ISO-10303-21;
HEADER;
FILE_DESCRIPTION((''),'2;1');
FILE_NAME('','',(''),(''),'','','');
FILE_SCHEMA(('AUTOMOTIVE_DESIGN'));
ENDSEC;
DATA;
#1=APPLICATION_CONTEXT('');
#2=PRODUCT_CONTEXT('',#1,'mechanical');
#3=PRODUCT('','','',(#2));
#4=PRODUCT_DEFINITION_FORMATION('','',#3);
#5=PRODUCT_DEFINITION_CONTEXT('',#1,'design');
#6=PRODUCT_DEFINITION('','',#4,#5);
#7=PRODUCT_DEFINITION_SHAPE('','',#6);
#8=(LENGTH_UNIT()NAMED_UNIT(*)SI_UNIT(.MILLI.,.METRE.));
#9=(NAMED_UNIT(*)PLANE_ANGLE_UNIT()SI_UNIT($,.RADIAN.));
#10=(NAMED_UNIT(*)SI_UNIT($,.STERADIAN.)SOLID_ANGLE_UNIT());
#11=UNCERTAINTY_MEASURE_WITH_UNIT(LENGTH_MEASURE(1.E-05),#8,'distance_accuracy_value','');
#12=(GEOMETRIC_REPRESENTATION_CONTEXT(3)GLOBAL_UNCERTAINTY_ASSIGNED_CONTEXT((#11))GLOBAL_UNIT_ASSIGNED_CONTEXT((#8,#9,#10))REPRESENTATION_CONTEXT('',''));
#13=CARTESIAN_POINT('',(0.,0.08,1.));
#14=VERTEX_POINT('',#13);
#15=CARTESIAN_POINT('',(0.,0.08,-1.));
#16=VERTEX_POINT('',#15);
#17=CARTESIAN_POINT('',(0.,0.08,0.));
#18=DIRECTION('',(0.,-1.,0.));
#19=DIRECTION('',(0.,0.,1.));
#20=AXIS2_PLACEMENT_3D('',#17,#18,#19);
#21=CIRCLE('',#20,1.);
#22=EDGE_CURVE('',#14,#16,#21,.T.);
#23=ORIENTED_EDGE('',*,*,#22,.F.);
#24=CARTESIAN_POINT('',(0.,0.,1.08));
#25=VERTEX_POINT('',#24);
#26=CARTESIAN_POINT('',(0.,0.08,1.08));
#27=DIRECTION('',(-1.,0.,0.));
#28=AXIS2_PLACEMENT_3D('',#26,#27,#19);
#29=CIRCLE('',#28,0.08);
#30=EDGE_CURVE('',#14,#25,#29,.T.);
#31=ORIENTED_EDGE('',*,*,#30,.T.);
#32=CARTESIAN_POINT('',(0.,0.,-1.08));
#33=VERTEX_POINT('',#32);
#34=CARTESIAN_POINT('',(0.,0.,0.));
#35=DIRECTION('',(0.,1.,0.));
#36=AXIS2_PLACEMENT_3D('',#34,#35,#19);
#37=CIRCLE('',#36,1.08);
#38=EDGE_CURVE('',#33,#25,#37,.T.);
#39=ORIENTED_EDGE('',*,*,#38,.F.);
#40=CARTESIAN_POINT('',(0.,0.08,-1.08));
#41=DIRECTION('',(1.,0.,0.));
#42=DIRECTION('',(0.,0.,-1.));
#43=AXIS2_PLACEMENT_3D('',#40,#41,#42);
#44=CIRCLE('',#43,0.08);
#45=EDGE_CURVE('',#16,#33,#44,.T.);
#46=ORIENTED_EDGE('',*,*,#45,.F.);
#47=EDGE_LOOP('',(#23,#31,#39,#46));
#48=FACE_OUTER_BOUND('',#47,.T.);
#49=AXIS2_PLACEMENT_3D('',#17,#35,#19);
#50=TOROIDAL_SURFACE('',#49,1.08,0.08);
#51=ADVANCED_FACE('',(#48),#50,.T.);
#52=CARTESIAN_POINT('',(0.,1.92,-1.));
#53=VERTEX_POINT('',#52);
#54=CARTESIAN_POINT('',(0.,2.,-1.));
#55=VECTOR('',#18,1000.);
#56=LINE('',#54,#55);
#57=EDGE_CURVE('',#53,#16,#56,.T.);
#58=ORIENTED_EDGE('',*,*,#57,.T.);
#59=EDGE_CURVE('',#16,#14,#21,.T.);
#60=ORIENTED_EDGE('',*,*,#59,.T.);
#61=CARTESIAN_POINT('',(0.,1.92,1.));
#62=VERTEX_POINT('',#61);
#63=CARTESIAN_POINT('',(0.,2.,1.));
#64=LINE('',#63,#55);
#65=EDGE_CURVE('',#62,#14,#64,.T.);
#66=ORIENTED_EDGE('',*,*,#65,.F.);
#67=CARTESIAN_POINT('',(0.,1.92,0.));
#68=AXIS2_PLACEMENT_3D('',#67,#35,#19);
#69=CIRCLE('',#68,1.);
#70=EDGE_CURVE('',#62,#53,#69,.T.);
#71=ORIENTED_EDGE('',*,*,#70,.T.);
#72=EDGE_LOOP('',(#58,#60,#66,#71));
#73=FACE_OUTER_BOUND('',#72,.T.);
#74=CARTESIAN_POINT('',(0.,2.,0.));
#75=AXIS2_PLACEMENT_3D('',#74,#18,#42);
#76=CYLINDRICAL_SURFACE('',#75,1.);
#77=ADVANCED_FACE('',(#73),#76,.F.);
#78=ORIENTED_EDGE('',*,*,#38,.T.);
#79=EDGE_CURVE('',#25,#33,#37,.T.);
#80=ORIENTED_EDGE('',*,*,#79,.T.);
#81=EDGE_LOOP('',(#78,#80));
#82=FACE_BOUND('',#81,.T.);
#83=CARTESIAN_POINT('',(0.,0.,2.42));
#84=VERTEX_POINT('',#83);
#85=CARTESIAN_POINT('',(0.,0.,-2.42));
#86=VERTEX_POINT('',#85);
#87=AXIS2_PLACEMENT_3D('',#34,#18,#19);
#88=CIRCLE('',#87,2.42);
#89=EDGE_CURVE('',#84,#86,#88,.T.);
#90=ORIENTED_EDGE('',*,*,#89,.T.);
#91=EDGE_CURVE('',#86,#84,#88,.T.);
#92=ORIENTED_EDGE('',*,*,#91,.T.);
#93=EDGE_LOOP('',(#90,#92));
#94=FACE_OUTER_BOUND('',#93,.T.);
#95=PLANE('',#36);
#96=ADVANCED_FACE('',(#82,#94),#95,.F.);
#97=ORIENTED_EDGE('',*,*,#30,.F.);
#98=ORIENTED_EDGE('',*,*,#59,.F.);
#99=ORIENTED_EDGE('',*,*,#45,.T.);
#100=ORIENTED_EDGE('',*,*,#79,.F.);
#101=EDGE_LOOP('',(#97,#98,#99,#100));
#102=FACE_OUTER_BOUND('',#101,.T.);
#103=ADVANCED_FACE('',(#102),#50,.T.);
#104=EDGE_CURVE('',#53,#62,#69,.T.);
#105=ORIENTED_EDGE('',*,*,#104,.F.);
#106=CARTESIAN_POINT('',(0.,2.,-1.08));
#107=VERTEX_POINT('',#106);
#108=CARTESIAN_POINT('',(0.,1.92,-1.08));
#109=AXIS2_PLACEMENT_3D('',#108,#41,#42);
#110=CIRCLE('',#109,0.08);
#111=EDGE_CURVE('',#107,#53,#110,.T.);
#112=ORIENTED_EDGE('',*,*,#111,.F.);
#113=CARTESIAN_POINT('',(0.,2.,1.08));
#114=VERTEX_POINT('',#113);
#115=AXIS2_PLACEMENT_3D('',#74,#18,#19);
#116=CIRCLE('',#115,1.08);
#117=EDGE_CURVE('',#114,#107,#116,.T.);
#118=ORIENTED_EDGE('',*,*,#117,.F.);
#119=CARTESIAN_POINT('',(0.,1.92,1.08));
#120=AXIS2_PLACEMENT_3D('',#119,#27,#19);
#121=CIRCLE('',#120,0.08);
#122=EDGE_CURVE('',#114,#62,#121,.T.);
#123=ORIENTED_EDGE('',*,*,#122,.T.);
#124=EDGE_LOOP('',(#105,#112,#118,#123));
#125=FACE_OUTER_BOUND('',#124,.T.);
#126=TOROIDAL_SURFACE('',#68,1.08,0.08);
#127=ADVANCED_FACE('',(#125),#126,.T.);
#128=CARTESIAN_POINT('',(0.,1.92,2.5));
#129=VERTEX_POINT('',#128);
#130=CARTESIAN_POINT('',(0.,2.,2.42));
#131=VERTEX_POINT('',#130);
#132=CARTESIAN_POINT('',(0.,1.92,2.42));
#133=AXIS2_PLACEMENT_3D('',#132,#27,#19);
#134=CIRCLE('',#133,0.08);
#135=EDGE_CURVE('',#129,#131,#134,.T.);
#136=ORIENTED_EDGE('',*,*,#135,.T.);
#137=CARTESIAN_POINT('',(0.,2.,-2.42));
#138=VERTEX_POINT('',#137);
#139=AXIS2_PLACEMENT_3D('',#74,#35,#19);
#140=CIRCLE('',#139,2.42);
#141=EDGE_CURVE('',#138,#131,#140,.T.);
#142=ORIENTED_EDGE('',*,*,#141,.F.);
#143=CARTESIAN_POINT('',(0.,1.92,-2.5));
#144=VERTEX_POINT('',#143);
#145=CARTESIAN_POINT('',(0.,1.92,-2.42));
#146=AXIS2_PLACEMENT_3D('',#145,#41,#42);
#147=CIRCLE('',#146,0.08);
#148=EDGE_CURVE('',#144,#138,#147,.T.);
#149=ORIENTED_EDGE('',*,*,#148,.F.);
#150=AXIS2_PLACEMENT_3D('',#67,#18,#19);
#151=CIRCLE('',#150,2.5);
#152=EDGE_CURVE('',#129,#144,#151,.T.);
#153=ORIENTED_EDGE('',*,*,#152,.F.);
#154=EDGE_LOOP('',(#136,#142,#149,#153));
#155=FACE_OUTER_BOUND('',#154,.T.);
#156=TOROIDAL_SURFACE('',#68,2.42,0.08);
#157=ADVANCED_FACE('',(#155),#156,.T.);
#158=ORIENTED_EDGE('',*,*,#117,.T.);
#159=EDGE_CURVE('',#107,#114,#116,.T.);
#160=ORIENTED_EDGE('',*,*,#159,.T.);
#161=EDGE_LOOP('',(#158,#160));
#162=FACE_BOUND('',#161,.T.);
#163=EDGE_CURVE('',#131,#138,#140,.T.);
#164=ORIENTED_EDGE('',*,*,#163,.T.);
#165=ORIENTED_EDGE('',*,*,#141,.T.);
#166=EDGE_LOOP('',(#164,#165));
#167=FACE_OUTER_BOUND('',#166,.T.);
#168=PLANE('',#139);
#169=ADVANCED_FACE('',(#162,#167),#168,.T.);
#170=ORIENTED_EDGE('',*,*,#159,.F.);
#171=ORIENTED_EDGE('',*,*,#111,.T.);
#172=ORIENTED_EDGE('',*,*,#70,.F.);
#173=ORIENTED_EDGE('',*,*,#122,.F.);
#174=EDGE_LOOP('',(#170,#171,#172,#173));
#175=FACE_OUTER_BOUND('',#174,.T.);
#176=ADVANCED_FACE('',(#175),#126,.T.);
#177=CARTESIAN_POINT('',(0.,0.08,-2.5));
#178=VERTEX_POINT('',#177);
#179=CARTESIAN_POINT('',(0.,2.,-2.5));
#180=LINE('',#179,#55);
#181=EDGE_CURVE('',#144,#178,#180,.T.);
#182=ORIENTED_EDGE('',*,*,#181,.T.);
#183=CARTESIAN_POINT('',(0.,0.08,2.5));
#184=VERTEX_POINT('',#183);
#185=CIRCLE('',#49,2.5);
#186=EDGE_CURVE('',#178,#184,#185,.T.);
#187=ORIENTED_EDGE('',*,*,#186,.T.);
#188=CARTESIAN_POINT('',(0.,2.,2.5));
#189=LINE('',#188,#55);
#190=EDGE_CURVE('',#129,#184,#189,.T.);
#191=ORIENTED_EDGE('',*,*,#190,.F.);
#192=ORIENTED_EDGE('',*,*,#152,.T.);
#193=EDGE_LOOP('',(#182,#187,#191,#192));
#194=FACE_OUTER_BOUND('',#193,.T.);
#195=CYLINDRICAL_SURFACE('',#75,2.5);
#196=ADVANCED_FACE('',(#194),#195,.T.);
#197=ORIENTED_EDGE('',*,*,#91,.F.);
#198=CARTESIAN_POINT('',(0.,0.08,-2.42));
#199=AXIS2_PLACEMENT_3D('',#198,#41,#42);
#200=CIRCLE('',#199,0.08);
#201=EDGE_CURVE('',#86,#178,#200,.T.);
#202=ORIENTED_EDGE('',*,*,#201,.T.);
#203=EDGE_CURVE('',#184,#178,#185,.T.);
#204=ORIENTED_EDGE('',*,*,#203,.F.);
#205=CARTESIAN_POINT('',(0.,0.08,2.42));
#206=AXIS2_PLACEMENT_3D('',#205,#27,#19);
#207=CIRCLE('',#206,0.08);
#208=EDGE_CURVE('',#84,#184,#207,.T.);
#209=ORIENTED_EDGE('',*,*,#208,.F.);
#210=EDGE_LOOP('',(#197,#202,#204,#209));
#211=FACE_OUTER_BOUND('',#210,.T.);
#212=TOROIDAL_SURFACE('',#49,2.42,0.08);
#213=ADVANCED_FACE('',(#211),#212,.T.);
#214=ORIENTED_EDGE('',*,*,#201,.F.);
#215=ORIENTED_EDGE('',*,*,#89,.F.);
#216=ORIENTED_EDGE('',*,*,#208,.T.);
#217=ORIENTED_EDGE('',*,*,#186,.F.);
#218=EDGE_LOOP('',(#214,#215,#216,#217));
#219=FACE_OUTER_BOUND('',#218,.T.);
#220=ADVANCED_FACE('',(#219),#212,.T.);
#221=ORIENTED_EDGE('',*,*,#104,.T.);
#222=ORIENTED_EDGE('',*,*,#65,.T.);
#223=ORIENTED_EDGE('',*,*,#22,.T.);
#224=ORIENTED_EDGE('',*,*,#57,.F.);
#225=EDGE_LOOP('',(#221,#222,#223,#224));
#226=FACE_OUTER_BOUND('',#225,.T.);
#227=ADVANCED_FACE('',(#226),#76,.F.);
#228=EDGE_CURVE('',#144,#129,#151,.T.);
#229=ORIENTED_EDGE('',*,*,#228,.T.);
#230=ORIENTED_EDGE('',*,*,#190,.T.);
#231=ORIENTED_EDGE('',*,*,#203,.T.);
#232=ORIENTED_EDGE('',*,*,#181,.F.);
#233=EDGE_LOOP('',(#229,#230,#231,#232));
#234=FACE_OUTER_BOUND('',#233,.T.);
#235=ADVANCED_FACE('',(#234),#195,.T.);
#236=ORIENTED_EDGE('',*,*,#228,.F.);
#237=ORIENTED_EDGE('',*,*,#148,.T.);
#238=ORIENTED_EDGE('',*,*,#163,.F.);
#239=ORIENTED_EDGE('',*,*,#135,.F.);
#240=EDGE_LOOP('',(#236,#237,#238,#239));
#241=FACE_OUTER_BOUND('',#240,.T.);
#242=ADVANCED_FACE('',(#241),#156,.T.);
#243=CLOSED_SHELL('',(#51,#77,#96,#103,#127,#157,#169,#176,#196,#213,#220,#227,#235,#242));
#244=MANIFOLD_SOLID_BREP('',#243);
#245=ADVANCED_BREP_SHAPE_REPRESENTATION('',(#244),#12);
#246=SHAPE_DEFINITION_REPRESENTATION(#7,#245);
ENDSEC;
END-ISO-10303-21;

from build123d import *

# Parameters (mm, degrees)
SKETCH_1_R       = 2.5
SKETCH_1_R_2     = 1
EXTRUDE_1_DEPTH  = 2
FILLET_R0_08_1_R = 0.08


with BuildPart() as part:
    # 草图1 → 凸台-拉伸1 (new body)
    with BuildSketch(Plane(origin=(0, 0, 0), x_dir=(1, 0, 0), z_dir=(0, 1, 0))):
        with Locations(Location((0, 0, 0), (0, 0, 270))):
            Circle(SKETCH_1_R)
        with Locations(Location((0, 0, 0), (0, 0, 270))):
            Circle(SKETCH_1_R_2, mode=Mode.SUBTRACT)
    extrude(amount=EXTRUDE_1_DEPTH)

    # R0.08 圆角1
    fillet_r0_08_1_edges = [part.edges().sort_by_distance(p)[0] for p in [
        (0, 0, -2.5),
        (0, 2, -2.5),
        (0, 0, -1),
        (0, 2, -1),
    ]]
    fillet(fillet_r0_08_1_edges, radius=FILLET_R0_08_1_R)


solid = part.part
